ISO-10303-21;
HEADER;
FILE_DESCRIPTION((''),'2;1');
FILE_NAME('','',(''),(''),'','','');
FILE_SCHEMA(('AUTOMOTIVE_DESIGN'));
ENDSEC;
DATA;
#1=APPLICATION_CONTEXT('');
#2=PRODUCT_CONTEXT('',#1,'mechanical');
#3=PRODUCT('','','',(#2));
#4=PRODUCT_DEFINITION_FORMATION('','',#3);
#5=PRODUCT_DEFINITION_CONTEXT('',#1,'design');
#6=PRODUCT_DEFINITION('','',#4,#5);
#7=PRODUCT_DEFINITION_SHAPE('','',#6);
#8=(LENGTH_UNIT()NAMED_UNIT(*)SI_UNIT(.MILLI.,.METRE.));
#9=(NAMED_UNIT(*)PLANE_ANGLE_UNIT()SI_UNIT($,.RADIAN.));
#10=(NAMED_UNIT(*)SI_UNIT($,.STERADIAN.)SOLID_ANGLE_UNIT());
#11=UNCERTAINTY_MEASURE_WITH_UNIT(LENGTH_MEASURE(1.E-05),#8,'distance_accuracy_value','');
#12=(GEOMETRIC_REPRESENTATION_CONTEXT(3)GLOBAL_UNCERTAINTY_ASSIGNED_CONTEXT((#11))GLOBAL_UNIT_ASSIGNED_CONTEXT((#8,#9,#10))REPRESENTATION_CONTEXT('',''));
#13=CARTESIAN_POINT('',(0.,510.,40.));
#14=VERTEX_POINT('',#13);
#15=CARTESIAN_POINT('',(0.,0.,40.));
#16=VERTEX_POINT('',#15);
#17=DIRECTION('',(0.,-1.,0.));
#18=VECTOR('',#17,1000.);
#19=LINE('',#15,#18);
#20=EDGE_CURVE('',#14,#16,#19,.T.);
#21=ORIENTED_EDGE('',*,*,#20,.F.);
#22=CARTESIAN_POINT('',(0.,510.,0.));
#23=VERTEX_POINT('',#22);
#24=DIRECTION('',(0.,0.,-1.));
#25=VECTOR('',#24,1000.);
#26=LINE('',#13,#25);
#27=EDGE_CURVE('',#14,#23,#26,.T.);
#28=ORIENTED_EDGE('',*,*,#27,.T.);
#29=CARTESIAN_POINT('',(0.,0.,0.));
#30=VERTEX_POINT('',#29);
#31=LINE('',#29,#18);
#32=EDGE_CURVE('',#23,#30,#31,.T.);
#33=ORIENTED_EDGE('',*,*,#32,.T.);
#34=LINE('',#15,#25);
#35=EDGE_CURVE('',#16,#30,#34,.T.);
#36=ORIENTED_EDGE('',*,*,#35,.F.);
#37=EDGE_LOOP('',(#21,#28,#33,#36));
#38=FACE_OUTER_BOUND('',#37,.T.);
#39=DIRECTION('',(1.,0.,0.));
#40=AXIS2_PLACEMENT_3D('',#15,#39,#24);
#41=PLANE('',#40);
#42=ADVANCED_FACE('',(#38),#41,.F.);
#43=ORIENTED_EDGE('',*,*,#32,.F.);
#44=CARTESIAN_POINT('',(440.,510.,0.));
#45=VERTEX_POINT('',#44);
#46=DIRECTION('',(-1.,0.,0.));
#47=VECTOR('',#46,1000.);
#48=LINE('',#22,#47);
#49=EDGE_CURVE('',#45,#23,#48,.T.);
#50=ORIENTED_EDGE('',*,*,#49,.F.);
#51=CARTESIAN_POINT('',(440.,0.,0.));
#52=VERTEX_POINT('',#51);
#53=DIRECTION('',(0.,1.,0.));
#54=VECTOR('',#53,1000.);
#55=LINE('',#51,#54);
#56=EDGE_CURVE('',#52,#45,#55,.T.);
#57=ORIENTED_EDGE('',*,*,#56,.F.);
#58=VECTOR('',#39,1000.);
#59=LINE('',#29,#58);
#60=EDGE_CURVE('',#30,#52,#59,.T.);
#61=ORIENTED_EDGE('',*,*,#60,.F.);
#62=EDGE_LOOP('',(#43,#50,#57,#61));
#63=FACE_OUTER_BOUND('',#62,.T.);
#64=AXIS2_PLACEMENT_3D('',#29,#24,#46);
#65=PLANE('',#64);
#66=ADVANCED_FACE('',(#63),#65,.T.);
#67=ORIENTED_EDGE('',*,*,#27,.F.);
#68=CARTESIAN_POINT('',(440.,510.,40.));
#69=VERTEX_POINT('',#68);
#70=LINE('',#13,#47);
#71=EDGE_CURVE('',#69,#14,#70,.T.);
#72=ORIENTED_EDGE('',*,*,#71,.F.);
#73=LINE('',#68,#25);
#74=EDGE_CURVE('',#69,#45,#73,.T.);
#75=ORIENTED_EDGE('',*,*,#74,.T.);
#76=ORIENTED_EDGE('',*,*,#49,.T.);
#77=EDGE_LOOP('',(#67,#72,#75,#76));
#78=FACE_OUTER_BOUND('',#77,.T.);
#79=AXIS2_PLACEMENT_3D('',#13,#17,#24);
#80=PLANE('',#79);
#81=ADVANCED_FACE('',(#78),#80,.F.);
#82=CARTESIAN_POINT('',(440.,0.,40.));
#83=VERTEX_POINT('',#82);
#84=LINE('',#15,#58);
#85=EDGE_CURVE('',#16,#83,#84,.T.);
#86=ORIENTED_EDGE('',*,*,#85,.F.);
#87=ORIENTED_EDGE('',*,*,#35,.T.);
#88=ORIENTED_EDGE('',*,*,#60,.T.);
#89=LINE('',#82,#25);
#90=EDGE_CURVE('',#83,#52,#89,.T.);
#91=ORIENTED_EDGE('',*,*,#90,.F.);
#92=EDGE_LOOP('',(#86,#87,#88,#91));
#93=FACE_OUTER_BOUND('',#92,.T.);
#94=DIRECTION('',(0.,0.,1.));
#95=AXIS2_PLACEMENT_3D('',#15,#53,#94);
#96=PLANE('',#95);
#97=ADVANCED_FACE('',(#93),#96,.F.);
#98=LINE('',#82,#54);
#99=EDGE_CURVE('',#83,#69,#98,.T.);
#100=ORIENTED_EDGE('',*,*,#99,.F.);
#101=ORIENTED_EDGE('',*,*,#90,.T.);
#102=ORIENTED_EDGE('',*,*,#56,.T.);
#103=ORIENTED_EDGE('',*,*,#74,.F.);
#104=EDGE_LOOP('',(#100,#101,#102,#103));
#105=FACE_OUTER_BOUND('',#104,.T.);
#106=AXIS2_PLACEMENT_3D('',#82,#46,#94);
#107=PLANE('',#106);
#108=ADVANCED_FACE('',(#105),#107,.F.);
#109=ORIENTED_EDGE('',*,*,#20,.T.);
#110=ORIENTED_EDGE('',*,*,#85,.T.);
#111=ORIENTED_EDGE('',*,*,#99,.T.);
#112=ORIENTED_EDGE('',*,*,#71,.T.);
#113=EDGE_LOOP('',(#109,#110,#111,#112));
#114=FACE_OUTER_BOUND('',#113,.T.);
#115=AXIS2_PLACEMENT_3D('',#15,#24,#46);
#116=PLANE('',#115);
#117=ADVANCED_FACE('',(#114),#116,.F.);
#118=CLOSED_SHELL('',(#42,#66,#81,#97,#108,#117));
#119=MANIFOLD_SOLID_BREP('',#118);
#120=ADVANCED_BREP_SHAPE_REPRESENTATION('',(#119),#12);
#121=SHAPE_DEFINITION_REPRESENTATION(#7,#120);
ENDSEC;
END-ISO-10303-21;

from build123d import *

# Parameters (mm, degrees)
SKETCH1_W           = 440
SKETCH1_H           = 510
BOSS_EXTRUDE1_DEPTH = 40


with BuildPart() as part:
    # Sketch1 → Boss-Extrude1 (new body)
    with BuildSketch(Plane.XY):
        with Locations((220, 255)):
            Rectangle(SKETCH1_W, SKETCH1_H)
    extrude(amount=BOSS_EXTRUDE1_DEPTH)


solid = part.part
